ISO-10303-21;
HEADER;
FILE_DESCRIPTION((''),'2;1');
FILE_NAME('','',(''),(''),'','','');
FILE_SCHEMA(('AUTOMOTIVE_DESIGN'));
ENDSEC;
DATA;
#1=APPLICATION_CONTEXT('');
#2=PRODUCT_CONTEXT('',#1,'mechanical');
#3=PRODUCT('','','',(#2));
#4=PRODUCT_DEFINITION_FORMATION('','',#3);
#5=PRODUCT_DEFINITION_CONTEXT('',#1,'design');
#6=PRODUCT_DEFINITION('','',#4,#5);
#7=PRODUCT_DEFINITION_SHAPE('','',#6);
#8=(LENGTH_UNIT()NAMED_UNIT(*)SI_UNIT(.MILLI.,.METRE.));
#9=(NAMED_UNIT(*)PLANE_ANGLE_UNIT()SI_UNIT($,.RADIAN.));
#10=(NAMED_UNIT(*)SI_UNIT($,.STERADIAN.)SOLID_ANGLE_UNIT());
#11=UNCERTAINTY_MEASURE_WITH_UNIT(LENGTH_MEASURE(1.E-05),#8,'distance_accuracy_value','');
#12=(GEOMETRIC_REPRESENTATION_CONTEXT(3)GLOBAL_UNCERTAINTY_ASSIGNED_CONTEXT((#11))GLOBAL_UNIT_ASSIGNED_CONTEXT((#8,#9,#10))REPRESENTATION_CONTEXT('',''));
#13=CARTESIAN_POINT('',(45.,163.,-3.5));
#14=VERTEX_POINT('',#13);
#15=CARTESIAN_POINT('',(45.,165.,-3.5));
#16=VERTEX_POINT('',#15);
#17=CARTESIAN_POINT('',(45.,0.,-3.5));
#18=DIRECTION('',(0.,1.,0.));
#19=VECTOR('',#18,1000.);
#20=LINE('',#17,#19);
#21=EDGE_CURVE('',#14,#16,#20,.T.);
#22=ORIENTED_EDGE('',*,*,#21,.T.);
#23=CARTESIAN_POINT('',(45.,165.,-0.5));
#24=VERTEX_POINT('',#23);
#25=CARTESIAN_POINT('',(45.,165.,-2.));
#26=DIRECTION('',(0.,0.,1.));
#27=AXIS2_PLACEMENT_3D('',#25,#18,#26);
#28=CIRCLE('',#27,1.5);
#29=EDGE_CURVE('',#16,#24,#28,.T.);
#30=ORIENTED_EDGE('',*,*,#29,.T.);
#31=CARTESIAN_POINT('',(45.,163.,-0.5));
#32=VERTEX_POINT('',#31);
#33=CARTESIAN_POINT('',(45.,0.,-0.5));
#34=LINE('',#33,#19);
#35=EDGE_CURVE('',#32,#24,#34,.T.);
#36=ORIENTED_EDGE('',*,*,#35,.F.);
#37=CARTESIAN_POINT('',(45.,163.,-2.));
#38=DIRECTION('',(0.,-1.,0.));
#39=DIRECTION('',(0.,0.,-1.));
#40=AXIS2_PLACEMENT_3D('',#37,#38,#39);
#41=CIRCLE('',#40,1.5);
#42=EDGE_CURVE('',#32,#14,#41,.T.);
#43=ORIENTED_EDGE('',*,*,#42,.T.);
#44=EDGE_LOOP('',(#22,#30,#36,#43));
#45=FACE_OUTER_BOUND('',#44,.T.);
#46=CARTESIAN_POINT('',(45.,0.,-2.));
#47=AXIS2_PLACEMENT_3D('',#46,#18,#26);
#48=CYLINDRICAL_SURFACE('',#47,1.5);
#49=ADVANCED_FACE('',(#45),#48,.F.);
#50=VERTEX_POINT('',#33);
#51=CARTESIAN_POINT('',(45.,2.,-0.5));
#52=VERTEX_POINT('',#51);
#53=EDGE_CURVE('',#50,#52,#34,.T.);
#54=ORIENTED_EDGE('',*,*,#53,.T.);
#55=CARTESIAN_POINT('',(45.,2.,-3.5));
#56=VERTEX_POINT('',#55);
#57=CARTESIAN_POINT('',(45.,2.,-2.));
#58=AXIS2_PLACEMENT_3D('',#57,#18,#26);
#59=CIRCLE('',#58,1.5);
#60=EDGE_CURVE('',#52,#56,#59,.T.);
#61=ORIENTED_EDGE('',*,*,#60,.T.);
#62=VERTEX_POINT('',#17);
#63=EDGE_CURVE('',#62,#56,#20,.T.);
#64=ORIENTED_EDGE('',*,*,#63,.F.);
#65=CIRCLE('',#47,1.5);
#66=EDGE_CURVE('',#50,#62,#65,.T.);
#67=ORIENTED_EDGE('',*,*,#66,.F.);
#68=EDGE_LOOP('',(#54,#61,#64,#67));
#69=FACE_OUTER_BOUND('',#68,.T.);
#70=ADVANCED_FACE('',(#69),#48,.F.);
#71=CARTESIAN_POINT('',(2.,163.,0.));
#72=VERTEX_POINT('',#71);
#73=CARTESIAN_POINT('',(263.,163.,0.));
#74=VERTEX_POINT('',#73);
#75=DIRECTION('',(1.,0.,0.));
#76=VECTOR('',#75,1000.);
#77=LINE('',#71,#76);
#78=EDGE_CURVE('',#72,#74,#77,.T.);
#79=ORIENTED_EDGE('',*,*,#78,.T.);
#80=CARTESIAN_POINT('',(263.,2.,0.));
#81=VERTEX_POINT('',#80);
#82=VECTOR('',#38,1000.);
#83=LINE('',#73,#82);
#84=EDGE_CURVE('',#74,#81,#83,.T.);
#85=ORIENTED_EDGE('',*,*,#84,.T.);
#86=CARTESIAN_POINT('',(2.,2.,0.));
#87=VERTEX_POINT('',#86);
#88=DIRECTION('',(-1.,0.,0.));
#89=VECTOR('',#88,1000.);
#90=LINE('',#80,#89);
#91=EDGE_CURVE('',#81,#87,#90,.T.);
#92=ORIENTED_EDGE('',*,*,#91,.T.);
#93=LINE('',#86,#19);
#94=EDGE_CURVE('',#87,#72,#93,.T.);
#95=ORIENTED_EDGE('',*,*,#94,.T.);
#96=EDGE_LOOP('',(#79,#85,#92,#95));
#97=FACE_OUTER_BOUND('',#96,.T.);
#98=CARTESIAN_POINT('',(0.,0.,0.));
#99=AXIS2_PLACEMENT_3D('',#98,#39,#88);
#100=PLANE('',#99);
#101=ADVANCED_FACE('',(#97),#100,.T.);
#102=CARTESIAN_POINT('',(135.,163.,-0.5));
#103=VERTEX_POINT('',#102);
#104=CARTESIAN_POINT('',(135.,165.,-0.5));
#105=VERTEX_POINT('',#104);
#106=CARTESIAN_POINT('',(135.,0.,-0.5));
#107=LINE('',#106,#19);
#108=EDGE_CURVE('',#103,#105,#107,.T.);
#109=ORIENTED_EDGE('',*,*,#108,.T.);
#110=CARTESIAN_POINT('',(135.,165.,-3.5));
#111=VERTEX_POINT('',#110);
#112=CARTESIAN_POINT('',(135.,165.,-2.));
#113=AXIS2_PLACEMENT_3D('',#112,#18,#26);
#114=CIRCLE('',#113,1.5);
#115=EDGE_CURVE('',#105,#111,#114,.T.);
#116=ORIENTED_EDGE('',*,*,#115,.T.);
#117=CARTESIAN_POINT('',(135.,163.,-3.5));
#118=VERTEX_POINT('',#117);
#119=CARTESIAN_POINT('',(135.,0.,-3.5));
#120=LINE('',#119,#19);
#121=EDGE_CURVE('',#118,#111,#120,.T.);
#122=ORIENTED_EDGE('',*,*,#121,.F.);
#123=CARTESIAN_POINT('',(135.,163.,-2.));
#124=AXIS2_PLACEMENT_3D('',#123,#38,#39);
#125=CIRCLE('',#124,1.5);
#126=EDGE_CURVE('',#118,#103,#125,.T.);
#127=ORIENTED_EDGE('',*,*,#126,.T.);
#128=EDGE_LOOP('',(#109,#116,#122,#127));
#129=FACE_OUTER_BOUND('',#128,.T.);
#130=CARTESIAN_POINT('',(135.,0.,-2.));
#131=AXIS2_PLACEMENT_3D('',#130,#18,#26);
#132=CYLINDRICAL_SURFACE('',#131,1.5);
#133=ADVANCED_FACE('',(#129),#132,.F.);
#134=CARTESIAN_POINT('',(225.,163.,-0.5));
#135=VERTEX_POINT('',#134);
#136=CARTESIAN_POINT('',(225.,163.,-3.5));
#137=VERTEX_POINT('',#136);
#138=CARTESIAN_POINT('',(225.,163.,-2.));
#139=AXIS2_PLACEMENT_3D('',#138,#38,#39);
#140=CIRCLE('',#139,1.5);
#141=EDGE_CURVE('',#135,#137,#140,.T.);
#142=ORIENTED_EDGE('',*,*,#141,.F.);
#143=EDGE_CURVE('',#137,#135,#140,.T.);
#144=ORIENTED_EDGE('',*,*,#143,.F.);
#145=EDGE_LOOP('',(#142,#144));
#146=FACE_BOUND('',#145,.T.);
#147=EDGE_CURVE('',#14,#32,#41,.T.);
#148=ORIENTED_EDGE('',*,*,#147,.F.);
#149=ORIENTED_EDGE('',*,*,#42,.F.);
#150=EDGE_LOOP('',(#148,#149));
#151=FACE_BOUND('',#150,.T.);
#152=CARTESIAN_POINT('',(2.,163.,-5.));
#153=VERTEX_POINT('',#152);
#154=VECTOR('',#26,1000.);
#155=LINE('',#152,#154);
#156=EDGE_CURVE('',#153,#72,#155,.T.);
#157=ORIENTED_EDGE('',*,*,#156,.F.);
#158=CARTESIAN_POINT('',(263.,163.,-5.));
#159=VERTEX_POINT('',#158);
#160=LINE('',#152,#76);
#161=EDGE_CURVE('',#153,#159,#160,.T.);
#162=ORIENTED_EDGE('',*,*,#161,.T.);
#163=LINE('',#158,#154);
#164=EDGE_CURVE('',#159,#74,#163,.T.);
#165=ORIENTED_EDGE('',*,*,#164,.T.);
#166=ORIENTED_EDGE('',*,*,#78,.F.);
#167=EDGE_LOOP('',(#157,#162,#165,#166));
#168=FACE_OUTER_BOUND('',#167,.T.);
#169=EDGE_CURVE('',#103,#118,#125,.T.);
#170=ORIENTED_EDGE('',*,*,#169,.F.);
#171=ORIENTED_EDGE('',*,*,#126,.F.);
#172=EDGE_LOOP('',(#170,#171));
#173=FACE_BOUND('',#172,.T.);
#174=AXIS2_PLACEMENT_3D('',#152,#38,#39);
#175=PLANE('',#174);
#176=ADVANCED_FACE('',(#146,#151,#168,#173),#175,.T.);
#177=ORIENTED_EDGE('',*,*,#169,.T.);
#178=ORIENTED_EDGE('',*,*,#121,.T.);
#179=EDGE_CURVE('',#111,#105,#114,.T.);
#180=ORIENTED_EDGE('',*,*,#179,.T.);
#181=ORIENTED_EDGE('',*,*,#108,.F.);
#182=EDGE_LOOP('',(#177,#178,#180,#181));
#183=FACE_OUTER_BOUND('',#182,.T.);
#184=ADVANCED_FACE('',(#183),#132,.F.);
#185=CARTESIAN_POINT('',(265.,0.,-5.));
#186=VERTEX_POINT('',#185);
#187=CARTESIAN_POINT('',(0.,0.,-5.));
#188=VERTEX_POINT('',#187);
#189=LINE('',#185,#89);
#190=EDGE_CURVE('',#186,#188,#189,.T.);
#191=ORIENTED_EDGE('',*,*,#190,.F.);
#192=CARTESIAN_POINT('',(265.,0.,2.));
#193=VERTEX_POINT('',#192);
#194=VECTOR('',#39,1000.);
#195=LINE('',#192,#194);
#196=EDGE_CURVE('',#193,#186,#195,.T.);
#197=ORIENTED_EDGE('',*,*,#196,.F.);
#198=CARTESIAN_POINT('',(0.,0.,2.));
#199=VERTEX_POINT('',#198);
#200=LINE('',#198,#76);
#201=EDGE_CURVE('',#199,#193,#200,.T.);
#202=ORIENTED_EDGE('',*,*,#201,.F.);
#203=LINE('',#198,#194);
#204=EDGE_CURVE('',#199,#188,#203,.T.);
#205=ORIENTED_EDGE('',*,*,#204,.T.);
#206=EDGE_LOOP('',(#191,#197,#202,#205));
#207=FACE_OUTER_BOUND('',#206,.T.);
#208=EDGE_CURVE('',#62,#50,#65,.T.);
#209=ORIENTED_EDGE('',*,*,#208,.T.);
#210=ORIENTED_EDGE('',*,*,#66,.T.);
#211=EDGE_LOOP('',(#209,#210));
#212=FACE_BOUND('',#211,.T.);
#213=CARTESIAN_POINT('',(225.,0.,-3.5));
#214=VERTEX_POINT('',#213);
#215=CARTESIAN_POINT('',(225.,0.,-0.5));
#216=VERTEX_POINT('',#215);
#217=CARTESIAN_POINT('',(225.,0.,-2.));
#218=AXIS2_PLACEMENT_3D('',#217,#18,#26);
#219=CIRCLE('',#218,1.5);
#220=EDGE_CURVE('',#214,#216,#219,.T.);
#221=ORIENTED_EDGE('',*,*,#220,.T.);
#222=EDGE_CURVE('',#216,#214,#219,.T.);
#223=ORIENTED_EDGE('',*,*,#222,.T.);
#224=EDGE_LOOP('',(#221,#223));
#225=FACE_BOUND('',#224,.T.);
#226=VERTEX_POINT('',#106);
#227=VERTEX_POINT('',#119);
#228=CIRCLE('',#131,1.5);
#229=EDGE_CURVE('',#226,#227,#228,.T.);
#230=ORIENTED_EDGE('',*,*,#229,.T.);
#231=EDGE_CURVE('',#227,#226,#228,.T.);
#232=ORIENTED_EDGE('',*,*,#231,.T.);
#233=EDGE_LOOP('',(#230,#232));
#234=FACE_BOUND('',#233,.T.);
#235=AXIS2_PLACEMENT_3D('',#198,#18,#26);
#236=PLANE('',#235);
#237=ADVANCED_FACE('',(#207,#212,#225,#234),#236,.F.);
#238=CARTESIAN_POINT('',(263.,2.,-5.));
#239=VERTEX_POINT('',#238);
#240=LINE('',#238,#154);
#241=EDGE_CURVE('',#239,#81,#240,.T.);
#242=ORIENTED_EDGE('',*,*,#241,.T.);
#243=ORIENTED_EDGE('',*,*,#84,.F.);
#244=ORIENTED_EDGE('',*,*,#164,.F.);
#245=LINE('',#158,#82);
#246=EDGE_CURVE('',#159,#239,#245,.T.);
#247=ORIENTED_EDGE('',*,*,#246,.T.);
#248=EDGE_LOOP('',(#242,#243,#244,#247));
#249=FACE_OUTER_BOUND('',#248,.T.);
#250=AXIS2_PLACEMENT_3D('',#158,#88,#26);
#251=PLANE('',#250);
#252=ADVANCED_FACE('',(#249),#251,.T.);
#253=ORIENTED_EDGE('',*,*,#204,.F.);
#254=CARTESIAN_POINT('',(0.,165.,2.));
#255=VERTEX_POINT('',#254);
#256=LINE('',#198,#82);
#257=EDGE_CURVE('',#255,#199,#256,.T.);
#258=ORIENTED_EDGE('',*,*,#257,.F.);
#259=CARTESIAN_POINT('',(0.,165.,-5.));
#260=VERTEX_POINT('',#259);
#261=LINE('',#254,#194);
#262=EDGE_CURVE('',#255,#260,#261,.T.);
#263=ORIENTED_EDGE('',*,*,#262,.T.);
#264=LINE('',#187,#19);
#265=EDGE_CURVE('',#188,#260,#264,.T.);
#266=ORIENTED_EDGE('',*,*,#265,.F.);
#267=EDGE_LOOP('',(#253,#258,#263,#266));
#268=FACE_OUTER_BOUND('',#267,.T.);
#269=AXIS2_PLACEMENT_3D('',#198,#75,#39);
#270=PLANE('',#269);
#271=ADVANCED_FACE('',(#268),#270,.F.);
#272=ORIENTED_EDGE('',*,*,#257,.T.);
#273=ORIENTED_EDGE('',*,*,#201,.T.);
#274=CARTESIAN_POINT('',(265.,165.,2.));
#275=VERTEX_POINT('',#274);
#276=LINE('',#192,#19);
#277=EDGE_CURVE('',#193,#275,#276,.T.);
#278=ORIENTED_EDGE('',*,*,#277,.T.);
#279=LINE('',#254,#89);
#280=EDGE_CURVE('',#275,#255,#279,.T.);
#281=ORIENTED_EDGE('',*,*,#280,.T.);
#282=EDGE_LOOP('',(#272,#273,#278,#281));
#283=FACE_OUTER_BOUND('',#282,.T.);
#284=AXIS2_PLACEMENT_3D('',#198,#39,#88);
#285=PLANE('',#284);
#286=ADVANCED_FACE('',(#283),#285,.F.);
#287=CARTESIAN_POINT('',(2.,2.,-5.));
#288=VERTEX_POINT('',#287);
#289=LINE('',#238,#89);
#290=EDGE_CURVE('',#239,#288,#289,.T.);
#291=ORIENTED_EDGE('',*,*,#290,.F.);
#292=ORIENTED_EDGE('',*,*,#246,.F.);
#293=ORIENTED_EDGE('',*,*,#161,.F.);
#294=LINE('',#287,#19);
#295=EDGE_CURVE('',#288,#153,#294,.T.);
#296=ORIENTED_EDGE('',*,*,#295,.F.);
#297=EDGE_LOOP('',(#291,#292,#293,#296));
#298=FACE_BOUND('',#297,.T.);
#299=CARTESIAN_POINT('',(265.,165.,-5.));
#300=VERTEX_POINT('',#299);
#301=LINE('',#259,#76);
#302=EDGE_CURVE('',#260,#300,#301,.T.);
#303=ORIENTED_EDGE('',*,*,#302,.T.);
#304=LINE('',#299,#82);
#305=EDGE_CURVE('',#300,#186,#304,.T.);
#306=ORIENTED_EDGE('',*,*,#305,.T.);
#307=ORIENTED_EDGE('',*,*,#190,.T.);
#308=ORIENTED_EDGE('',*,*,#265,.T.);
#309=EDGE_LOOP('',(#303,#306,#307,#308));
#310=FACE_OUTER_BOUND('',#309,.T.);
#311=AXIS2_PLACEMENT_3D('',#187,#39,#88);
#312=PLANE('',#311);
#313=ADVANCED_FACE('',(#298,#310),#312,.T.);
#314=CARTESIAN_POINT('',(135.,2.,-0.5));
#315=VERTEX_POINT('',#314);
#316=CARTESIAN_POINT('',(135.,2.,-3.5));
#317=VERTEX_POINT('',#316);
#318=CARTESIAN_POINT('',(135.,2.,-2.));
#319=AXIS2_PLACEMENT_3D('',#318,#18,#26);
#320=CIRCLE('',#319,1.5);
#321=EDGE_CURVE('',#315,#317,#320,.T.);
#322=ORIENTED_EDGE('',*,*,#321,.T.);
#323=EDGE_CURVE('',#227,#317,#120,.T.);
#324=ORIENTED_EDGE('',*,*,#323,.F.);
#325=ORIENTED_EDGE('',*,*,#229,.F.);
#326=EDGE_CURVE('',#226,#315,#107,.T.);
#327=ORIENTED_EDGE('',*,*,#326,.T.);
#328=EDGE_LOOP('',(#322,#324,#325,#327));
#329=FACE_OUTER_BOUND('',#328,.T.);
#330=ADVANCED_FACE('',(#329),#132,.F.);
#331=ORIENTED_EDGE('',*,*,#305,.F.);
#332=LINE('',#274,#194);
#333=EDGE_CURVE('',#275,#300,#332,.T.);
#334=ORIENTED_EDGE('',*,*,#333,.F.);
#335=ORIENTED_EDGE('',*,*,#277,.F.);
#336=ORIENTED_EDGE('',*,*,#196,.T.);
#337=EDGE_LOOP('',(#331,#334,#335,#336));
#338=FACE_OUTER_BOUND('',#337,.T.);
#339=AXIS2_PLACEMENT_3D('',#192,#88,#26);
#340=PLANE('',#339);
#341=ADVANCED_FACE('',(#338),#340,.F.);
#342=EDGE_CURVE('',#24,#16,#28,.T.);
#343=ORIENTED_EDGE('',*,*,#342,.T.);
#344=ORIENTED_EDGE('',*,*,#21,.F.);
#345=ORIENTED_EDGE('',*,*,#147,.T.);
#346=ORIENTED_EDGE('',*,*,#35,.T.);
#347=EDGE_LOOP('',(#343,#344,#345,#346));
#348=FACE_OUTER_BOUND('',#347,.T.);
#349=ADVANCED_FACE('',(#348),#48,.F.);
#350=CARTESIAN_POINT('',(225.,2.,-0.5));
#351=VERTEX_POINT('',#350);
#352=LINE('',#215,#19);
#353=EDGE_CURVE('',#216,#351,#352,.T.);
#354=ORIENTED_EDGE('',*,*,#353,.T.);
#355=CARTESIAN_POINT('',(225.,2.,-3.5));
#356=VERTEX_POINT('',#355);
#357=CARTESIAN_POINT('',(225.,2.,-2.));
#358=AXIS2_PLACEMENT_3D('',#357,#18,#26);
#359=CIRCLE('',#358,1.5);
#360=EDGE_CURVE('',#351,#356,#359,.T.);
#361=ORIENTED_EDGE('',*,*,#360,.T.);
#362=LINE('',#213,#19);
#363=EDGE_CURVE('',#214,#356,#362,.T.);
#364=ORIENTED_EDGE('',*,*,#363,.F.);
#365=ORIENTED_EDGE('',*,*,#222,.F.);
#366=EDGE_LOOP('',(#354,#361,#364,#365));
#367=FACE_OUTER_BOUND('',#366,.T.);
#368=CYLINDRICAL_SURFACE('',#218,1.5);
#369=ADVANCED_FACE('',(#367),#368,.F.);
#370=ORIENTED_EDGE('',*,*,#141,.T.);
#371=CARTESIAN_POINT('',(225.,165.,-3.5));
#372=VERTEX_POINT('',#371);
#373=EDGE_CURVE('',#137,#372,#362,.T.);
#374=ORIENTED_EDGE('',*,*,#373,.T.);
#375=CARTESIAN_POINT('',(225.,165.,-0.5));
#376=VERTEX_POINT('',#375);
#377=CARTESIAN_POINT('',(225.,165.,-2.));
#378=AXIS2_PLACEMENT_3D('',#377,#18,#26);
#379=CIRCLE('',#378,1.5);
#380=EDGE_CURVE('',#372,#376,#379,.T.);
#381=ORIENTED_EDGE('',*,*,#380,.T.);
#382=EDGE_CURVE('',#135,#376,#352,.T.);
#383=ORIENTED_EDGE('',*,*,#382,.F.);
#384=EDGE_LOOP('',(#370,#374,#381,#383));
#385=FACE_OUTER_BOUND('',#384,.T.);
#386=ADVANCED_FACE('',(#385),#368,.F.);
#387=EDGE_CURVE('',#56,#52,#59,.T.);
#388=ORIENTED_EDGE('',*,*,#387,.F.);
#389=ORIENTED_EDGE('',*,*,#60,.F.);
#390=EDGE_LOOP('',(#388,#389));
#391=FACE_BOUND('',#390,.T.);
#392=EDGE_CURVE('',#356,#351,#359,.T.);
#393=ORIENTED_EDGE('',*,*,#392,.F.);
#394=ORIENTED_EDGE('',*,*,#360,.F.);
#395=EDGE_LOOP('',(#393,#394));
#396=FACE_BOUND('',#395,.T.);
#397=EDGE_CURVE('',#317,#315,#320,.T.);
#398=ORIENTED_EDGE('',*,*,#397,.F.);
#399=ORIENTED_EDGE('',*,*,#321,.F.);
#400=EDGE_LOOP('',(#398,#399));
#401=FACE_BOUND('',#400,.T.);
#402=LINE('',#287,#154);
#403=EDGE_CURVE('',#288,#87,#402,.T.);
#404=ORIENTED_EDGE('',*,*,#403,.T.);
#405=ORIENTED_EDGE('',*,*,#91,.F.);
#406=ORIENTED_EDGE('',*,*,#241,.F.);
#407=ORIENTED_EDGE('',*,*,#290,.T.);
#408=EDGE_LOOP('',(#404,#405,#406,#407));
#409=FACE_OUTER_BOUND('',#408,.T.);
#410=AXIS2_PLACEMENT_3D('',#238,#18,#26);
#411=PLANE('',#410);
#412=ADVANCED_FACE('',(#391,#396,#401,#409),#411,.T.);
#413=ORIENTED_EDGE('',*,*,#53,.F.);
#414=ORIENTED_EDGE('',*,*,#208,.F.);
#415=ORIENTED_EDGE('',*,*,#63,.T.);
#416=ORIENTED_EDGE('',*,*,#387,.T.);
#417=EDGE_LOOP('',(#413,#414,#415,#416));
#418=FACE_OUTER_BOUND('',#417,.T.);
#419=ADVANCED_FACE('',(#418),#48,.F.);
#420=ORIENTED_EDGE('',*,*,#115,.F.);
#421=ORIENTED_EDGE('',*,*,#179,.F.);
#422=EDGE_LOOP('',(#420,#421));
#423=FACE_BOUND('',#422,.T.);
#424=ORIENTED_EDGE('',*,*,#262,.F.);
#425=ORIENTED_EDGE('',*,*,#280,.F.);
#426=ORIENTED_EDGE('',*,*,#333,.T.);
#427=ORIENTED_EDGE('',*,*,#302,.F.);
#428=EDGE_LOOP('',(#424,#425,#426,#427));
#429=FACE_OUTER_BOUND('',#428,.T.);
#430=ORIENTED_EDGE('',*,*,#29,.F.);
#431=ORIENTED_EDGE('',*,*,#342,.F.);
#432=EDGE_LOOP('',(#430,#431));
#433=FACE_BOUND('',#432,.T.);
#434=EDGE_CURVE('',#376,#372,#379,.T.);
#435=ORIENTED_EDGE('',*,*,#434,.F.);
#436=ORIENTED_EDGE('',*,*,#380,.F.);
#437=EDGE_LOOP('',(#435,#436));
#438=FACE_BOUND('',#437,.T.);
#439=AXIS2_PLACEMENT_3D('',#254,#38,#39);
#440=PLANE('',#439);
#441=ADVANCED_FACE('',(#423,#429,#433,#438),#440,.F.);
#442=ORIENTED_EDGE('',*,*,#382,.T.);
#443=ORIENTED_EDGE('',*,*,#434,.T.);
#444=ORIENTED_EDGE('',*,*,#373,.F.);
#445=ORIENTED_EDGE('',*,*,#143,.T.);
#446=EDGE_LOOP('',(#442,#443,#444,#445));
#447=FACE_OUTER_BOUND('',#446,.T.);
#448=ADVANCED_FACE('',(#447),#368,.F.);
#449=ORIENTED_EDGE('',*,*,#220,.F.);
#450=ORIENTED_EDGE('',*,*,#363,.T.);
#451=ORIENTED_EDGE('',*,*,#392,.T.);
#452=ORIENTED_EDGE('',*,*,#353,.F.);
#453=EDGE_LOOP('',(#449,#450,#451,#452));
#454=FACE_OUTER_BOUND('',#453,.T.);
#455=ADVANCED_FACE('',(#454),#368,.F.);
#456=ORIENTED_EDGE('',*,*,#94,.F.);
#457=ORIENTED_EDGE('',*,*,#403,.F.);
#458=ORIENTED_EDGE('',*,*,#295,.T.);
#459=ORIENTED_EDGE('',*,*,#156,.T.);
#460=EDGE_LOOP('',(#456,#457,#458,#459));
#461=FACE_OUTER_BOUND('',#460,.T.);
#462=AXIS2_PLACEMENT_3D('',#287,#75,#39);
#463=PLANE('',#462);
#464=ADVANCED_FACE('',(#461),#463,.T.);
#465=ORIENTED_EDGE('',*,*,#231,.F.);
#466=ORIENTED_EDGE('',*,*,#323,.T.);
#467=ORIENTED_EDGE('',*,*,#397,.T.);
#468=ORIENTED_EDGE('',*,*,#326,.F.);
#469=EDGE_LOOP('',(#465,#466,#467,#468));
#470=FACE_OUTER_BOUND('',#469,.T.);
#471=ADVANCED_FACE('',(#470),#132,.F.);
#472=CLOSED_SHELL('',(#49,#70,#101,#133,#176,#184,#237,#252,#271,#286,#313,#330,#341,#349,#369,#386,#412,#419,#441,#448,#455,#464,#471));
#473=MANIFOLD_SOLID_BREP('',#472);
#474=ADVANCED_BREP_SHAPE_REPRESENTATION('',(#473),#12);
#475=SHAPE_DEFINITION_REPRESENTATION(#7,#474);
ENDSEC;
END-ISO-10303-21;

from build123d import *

# Parameters (mm, degrees)
SKETCH1_W           = 265
SKETCH1_H           = 165
BOSS_EXTRUDE1_DEPTH = 2
SKETCH2_W           = 265
SKETCH2_H           = 165
SKETCH2_W_2         = 261
SKETCH2_H_2         = 161
BOSS_EXTRUDE2_DEPTH = 5
SKETCH3_R           = 1.5
CUT_EXTRUDE1_DEPTH  = 313.209865315
LPATTERN1_COUNT     = 3
LPATTERN1_PITCH     = 90


with BuildPart() as part:
    # Sketch1 → Boss-Extrude1 (new body)
    with BuildSketch(Plane.XY):
        with Locations((132.5, 82.5)):
            Rectangle(SKETCH1_W, SKETCH1_H)
    extrude(amount=BOSS_EXTRUDE1_DEPTH)

    # Sketch2 → Boss-Extrude2 (add)
    with BuildSketch(Plane(origin=(0, 0, 0), x_dir=(-1, 0, 0), z_dir=(0, 0, -1))):
        with Locations((-132.5, 82.5)):
            Rectangle(SKETCH2_W, SKETCH2_H)
        with Locations((-132.5, 82.5)):
            Rectangle(SKETCH2_W_2, SKETCH2_H_2, mode=Mode.SUBTRACT)
    extrude(amount=BOSS_EXTRUDE2_DEPTH)

    # Sketch3 → Cut-Extrude1 (cut, through all)
    with BuildSketch(Plane(origin=(0, 165, 0), x_dir=(1, 0, 0), z_dir=(0, 1, 0))):
        with Locations(Location((225, 2, 0), (0, 0, 270))):
            Circle(SKETCH3_R)
    cut_extrude1 = extrude(amount=-CUT_EXTRUDE1_DEPTH, mode=Mode.SUBTRACT)

    # LPattern1: Cut-Extrude1 ×3
    with Locations(*[(-i * LPATTERN1_PITCH, 0, 0) for i in range(1, LPATTERN1_COUNT)]):
        add(cut_extrude1, mode=Mode.SUBTRACT)


solid = part.part
